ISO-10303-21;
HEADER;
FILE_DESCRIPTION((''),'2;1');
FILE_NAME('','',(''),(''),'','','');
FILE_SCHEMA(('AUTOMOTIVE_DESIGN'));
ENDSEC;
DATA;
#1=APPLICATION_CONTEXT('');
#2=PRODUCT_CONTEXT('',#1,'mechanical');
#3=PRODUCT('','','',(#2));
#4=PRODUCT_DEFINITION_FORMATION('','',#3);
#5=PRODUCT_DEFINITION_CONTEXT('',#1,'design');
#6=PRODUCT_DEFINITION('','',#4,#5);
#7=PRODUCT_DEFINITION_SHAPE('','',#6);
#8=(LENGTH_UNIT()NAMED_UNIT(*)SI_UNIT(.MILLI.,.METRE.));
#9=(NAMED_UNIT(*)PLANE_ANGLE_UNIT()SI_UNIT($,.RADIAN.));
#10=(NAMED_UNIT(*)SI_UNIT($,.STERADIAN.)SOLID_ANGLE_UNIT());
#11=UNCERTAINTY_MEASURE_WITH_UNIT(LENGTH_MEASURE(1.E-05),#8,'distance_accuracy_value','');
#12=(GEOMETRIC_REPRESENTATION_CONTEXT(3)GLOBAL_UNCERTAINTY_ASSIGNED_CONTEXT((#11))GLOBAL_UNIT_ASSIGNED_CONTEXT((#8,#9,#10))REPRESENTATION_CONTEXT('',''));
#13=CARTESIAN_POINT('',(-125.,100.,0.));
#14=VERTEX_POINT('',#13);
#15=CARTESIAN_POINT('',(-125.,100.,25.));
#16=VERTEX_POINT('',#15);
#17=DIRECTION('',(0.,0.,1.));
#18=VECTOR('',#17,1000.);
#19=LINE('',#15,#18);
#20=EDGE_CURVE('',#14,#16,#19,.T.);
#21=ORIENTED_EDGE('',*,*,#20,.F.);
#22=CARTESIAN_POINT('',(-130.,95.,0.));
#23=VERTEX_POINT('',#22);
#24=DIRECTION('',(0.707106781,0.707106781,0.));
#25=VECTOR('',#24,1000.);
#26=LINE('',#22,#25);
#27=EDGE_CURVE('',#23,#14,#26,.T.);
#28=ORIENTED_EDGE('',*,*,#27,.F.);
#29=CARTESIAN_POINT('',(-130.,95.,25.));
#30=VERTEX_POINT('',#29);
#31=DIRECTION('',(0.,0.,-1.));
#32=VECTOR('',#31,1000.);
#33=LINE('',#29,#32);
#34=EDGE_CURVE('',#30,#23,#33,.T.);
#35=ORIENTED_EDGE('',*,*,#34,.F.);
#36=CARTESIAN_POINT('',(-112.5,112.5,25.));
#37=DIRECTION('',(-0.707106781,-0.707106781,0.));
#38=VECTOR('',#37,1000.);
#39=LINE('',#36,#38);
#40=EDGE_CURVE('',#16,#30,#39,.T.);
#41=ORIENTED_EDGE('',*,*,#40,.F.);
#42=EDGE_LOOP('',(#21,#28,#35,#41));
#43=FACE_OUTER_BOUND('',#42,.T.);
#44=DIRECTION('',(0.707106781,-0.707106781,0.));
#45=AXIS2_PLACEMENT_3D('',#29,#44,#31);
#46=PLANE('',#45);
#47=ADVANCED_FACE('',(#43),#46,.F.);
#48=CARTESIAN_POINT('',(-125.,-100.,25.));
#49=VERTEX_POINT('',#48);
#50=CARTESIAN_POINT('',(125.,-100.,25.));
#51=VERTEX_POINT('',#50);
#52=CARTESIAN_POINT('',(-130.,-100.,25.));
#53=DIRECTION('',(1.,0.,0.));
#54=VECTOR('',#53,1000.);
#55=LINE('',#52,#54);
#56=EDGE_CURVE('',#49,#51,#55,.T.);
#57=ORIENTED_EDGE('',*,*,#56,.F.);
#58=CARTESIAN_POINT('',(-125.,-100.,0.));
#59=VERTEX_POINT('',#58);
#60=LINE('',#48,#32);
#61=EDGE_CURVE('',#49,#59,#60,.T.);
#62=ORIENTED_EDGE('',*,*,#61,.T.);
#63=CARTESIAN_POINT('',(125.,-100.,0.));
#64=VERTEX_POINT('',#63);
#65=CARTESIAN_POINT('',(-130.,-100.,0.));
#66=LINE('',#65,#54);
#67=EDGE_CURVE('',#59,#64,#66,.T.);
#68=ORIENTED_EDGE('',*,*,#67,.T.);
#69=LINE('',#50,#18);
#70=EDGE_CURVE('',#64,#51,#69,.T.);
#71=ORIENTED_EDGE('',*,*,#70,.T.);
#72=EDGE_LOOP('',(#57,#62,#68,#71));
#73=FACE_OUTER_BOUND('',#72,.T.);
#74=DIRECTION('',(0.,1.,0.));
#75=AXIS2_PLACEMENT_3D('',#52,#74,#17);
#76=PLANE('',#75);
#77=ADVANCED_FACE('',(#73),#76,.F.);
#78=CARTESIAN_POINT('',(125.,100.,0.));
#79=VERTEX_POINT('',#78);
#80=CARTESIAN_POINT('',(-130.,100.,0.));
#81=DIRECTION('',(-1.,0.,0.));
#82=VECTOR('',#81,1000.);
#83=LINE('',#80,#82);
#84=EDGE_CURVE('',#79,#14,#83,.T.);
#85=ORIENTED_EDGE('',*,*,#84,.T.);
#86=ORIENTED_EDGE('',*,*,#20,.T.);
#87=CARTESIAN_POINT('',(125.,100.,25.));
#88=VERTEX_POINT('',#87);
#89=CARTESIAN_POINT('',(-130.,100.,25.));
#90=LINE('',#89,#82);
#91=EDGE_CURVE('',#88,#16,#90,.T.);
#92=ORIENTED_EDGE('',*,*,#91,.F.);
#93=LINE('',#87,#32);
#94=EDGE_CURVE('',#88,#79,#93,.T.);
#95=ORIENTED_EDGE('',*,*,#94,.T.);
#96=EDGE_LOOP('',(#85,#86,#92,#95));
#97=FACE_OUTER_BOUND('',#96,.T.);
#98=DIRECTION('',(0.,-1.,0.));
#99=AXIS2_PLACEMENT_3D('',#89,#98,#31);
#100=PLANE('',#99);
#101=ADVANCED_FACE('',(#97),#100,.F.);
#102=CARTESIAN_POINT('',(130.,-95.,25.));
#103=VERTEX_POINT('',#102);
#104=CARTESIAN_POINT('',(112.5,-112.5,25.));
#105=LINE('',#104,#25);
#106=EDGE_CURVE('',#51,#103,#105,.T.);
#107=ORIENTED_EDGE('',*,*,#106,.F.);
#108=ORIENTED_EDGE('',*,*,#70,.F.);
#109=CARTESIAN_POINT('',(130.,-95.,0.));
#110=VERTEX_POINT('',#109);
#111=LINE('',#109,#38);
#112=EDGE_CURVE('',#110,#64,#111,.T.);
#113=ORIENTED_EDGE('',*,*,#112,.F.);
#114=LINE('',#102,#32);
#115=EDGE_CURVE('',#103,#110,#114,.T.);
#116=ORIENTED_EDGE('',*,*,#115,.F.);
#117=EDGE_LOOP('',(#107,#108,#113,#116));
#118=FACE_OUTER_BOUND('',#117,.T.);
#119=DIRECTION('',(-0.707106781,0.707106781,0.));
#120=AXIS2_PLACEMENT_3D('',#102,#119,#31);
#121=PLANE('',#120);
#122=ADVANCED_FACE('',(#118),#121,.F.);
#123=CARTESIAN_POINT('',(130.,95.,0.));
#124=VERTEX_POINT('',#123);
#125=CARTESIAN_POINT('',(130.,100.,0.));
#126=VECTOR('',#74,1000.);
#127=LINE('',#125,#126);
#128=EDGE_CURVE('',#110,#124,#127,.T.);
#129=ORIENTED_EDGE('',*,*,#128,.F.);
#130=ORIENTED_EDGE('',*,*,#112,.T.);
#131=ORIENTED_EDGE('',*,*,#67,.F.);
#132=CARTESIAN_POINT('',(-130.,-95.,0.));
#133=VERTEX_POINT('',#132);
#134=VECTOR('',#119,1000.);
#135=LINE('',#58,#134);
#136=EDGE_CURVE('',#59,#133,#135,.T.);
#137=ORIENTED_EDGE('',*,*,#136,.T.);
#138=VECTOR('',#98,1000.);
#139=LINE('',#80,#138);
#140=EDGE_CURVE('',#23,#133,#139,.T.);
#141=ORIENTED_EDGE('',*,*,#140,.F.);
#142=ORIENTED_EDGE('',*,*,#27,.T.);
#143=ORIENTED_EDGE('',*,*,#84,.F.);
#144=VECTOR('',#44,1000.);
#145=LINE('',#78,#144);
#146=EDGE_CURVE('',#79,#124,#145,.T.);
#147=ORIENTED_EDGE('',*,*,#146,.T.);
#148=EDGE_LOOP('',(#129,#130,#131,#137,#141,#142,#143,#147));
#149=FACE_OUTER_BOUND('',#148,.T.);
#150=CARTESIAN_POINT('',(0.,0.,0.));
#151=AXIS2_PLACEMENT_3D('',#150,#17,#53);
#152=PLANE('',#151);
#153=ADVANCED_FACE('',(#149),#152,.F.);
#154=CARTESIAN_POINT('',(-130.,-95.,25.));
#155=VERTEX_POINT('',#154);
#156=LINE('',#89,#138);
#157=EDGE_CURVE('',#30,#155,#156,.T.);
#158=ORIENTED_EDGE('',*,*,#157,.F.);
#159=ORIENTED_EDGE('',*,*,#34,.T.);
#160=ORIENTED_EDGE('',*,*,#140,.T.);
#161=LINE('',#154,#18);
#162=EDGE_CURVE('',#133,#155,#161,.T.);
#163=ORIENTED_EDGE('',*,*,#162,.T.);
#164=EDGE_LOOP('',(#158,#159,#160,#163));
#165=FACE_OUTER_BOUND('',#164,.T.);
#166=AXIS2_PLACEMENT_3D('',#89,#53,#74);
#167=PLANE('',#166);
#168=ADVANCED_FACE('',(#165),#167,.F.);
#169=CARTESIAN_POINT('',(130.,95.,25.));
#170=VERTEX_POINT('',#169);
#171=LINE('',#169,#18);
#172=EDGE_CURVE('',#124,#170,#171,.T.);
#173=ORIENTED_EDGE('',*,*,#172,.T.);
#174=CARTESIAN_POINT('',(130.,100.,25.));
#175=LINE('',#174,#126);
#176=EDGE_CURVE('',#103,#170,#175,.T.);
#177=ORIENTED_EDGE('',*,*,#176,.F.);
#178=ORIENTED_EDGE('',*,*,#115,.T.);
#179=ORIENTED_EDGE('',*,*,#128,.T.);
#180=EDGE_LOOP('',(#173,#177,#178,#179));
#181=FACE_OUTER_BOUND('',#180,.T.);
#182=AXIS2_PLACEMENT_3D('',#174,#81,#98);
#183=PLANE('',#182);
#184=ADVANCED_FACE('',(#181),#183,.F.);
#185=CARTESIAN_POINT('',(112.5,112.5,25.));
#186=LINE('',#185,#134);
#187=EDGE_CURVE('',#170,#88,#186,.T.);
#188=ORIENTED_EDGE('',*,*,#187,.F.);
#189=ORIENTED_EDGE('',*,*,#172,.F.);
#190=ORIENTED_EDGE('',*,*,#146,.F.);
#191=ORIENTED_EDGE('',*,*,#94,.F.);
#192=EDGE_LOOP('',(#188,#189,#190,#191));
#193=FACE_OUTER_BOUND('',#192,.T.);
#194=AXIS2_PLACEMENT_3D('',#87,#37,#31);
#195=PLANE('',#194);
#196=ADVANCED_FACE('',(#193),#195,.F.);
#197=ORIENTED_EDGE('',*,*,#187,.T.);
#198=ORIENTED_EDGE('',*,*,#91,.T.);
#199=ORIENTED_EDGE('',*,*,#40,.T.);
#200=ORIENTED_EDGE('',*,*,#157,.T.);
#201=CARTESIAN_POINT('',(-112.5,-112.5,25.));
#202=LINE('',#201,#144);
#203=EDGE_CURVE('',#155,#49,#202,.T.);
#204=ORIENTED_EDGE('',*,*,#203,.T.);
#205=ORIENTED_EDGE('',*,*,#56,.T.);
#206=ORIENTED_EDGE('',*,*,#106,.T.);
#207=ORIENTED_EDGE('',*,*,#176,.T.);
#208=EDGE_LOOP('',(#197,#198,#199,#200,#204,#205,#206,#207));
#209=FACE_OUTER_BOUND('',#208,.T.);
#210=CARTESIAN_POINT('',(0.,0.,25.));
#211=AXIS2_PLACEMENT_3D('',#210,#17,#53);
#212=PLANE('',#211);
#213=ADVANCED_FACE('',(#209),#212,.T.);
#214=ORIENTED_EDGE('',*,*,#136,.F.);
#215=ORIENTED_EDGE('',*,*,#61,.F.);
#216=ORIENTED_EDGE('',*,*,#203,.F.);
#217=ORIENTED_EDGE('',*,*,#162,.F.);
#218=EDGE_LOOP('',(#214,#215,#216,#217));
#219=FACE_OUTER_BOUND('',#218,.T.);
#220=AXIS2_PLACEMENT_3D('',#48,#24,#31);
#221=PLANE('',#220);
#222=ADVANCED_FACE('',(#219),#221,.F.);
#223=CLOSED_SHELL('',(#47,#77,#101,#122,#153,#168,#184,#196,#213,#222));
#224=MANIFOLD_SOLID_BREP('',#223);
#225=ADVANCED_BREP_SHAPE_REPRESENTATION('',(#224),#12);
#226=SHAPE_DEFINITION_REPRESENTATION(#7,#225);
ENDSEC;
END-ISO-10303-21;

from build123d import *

# Parameters (mm, degrees)
SKETCH_1_W      = 260
SKETCH_1_H      = 200
EXTRUDE_1_DEPTH = 25
CHAMFER_1_SIZE  = 5


with BuildPart() as part:
    # 草图1 → 凸台-拉伸1 (new body)
    with BuildSketch(Plane.XY):
        Rectangle(SKETCH_1_W, SKETCH_1_H)
    extrude(amount=EXTRUDE_1_DEPTH)

    # 倒角1
    chamfer_1_edges = [part.edges().sort_by_distance(p)[0] for p in [
        (130, -100, 12.5),
        (-130, -100, 12.5),
        (-130, 100, 12.5),
        (130, 100, 12.5),
    ]]
    chamfer(chamfer_1_edges, length=CHAMFER_1_SIZE)


solid = part.part
